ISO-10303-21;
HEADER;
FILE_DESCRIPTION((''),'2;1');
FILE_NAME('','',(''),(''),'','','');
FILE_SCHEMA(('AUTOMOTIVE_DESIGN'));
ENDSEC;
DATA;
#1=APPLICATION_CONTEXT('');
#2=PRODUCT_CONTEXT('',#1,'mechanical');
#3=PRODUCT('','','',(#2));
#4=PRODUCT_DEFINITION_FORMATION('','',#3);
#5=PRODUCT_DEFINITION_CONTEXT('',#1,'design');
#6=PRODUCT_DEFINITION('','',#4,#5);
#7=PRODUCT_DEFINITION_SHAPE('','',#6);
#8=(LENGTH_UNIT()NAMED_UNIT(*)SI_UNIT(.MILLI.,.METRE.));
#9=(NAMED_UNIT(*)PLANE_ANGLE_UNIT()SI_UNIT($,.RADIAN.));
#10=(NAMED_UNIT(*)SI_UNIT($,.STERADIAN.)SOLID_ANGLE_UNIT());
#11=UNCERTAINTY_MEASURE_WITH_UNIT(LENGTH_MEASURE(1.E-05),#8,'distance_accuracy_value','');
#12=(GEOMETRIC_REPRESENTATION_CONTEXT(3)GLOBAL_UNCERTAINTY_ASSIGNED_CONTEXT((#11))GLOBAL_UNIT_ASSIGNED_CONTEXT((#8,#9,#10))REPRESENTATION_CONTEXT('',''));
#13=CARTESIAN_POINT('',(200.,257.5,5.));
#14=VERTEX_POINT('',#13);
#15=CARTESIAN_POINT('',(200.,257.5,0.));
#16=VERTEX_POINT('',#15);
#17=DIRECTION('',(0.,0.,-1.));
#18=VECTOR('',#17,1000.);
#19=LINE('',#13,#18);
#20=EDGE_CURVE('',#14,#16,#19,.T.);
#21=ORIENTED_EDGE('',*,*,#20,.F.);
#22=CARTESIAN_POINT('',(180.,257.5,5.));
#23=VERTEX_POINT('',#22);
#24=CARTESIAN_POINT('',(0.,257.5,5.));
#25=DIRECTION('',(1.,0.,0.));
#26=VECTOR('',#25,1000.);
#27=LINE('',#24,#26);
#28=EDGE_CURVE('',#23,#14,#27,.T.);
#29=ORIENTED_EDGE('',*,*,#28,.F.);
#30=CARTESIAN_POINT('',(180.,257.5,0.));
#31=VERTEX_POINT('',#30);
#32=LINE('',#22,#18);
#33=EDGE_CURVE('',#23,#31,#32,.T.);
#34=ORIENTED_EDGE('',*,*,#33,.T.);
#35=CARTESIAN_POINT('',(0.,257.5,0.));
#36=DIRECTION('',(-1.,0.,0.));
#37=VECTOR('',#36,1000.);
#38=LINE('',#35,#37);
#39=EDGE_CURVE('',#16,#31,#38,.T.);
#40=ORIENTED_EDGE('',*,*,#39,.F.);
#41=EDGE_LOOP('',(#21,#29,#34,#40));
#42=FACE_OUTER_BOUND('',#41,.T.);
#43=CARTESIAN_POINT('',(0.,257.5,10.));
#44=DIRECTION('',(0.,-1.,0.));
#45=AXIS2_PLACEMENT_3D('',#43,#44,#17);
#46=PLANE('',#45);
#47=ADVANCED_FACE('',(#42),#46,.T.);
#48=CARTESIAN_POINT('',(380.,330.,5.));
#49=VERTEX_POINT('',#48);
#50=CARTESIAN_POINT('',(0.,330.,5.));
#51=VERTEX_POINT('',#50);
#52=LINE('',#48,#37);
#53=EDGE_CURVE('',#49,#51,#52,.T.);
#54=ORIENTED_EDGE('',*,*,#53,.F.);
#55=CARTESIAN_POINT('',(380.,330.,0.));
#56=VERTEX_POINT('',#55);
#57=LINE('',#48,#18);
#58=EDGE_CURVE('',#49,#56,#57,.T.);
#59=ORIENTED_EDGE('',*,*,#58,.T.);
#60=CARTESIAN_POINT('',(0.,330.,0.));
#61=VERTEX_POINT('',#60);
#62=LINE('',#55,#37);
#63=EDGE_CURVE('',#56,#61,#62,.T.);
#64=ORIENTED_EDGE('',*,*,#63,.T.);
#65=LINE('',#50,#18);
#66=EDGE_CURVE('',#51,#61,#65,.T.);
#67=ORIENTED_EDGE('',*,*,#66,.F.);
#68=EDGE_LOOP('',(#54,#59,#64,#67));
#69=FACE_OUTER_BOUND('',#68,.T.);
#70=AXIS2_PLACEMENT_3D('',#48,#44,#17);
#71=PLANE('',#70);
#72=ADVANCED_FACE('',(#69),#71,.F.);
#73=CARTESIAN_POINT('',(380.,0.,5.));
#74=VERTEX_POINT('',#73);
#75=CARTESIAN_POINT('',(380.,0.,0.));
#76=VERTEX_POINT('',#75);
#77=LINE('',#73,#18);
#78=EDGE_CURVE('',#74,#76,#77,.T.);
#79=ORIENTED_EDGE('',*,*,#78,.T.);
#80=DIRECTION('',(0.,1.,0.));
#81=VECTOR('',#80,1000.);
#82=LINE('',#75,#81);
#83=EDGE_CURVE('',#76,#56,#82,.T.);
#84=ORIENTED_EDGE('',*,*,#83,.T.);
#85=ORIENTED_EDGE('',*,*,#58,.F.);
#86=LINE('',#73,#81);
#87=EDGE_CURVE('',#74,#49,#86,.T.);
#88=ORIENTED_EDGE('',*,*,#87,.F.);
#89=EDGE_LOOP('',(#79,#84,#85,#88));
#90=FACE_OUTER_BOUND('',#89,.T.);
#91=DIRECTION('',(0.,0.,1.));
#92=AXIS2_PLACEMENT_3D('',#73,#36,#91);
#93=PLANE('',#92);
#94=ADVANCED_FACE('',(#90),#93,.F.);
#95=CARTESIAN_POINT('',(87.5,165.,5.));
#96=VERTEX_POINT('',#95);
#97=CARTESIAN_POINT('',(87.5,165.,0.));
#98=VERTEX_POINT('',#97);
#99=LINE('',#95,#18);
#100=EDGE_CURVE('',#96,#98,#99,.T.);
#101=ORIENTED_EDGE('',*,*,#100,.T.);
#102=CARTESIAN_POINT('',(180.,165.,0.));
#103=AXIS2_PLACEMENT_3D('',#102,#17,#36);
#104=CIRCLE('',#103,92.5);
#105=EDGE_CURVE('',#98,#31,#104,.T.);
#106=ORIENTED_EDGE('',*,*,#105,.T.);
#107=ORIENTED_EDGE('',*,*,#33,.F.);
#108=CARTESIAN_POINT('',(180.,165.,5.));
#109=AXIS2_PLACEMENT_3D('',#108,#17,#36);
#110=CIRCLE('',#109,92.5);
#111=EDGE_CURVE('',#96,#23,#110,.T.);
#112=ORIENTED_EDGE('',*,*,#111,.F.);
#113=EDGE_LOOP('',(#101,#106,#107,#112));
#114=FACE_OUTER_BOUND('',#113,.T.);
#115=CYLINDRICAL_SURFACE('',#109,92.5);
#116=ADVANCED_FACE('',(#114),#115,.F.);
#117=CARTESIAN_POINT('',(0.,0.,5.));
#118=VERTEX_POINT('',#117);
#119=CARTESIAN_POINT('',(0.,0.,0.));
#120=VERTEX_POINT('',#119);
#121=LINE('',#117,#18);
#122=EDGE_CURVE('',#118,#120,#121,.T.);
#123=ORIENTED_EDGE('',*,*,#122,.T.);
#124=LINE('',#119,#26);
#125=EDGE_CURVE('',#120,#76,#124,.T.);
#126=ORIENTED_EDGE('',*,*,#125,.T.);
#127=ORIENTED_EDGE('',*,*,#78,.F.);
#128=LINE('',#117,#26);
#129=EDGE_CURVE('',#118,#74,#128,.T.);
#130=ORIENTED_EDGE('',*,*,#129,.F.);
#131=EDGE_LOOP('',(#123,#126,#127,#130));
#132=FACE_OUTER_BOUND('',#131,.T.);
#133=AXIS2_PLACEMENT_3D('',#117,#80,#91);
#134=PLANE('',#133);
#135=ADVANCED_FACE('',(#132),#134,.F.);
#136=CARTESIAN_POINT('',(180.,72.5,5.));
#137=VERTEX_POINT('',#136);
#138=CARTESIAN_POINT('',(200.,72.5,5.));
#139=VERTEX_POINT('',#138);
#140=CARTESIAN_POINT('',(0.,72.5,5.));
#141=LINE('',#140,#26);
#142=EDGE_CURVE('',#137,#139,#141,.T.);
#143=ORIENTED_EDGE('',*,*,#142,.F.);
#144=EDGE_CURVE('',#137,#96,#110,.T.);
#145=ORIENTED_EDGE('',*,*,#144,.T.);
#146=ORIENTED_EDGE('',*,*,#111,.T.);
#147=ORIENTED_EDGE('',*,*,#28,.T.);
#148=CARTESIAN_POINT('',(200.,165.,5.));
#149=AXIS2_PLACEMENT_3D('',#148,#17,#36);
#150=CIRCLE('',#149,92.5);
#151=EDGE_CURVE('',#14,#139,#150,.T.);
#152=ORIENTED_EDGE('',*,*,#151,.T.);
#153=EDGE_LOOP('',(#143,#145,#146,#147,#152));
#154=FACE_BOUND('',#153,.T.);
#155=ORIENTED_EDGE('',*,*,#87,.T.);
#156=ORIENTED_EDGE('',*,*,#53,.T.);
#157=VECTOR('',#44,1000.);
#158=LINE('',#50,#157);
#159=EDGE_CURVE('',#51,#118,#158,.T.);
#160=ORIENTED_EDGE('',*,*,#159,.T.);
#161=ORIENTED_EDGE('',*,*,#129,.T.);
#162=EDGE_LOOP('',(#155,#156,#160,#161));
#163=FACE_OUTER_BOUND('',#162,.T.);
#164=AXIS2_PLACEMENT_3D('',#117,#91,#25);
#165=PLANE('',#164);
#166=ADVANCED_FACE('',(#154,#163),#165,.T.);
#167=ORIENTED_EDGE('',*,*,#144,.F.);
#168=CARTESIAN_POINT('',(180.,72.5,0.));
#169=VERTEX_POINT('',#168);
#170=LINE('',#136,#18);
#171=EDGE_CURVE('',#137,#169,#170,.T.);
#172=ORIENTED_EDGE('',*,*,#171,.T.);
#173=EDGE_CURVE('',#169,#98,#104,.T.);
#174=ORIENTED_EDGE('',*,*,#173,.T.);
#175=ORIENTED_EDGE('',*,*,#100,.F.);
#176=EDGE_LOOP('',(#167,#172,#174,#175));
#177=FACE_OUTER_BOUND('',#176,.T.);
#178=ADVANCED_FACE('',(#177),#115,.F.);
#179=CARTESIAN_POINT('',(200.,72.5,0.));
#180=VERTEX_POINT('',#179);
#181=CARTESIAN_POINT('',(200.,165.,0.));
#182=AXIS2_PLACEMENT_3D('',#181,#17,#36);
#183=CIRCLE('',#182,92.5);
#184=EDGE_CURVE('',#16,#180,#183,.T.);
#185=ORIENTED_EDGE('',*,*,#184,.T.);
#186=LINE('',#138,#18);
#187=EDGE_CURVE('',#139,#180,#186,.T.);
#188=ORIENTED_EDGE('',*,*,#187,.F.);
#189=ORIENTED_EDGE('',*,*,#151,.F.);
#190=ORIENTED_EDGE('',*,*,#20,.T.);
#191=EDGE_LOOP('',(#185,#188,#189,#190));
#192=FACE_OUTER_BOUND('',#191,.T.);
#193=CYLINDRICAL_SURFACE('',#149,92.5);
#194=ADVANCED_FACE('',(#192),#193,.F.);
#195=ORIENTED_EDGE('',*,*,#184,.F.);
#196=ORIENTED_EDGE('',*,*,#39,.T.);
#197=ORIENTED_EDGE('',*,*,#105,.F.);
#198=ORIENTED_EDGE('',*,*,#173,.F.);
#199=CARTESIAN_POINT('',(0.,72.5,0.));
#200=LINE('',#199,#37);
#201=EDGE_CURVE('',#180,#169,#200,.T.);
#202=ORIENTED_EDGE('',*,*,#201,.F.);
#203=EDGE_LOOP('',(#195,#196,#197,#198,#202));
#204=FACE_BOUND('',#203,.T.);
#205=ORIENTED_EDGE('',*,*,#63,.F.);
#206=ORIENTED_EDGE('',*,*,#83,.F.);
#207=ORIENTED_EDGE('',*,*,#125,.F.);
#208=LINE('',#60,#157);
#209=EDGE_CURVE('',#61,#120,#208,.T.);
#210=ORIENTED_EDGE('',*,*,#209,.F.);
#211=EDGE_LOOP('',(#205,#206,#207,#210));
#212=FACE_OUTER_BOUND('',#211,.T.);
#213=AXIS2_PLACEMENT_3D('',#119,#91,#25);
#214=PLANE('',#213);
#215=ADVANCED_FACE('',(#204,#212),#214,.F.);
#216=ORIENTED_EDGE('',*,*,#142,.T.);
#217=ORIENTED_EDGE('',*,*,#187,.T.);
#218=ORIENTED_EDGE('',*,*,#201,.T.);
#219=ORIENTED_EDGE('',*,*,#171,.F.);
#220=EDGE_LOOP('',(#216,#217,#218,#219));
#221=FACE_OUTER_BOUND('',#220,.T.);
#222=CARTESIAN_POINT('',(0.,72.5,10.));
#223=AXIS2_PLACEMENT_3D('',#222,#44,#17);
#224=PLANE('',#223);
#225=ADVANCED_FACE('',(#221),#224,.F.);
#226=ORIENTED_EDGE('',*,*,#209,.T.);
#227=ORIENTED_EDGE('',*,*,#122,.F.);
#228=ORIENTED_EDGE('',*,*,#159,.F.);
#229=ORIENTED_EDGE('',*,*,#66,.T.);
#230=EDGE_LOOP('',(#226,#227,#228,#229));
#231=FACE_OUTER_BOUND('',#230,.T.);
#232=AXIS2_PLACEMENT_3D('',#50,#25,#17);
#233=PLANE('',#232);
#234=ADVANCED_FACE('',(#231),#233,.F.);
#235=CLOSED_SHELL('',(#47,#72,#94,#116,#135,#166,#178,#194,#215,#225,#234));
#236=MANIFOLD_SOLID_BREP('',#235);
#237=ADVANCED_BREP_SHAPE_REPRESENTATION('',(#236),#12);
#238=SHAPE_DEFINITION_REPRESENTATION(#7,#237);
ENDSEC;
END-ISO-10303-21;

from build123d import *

# Parameters (mm, degrees)
SKETCH_1_W          = 380
SKETCH_1_H          = 330
EXTRUDE_1_DEPTH     = 5
CUT_EXTRUDE_1_DEPTH = 10
EXTRUDE_2_DEPTH     = 5


with BuildPart() as part:
    # 草图1 → 凸台-拉伸1 (new body)
    with BuildSketch(Plane.XY):
        with Locations((190, 165)):
            Rectangle(SKETCH_1_W, SKETCH_1_H)
    extrude(amount=EXTRUDE_1_DEPTH)

    # 草图2 → 切除-拉伸1 (cut)
    with BuildSketch(Plane(origin=(0, 0, 0), x_dir=(-1, 0, 0), z_dir=(0, 0, -1))):
        with BuildLine():
            Line((-210, 72.5), (-170, 72.5))
            ThreePointArc((-170, 72.5), (-77.5, 165), (-170, 257.5))
            Line((-170, 257.5), (-210, 257.5))
            ThreePointArc((-210, 257.5), (-302.5, 165), (-210, 72.5))
        make_face()
    extrude(amount=-CUT_EXTRUDE_1_DEPTH, mode=Mode.SUBTRACT)

    # 草图3 → 凸台-拉伸2 (add)
    with BuildSketch(Plane(origin=(0, 0, 0), x_dir=(-1, 0, 0), z_dir=(0, 0, -1))):
        with BuildLine():
            ThreePointArc((-210, 257.5), (-302.5, 165), (-210, 72.5))
            Line((-210, 72.5), (-200, 72.5))
            ThreePointArc((-200, 72.5), (-292.5, 165), (-200, 257.5))
            Line((-200, 257.5), (-210, 257.5))
        make_face()
        with BuildLine():
            ThreePointArc((-180, 257.5), (-87.5, 165), (-180, 72.5))
            Line((-180, 72.5), (-170, 72.5))
            ThreePointArc((-170, 72.5), (-77.5, 165), (-170, 257.5))
            Line((-170, 257.5), (-180, 257.5))
        make_face()
    extrude(amount=-EXTRUDE_2_DEPTH)


solid = part.part
